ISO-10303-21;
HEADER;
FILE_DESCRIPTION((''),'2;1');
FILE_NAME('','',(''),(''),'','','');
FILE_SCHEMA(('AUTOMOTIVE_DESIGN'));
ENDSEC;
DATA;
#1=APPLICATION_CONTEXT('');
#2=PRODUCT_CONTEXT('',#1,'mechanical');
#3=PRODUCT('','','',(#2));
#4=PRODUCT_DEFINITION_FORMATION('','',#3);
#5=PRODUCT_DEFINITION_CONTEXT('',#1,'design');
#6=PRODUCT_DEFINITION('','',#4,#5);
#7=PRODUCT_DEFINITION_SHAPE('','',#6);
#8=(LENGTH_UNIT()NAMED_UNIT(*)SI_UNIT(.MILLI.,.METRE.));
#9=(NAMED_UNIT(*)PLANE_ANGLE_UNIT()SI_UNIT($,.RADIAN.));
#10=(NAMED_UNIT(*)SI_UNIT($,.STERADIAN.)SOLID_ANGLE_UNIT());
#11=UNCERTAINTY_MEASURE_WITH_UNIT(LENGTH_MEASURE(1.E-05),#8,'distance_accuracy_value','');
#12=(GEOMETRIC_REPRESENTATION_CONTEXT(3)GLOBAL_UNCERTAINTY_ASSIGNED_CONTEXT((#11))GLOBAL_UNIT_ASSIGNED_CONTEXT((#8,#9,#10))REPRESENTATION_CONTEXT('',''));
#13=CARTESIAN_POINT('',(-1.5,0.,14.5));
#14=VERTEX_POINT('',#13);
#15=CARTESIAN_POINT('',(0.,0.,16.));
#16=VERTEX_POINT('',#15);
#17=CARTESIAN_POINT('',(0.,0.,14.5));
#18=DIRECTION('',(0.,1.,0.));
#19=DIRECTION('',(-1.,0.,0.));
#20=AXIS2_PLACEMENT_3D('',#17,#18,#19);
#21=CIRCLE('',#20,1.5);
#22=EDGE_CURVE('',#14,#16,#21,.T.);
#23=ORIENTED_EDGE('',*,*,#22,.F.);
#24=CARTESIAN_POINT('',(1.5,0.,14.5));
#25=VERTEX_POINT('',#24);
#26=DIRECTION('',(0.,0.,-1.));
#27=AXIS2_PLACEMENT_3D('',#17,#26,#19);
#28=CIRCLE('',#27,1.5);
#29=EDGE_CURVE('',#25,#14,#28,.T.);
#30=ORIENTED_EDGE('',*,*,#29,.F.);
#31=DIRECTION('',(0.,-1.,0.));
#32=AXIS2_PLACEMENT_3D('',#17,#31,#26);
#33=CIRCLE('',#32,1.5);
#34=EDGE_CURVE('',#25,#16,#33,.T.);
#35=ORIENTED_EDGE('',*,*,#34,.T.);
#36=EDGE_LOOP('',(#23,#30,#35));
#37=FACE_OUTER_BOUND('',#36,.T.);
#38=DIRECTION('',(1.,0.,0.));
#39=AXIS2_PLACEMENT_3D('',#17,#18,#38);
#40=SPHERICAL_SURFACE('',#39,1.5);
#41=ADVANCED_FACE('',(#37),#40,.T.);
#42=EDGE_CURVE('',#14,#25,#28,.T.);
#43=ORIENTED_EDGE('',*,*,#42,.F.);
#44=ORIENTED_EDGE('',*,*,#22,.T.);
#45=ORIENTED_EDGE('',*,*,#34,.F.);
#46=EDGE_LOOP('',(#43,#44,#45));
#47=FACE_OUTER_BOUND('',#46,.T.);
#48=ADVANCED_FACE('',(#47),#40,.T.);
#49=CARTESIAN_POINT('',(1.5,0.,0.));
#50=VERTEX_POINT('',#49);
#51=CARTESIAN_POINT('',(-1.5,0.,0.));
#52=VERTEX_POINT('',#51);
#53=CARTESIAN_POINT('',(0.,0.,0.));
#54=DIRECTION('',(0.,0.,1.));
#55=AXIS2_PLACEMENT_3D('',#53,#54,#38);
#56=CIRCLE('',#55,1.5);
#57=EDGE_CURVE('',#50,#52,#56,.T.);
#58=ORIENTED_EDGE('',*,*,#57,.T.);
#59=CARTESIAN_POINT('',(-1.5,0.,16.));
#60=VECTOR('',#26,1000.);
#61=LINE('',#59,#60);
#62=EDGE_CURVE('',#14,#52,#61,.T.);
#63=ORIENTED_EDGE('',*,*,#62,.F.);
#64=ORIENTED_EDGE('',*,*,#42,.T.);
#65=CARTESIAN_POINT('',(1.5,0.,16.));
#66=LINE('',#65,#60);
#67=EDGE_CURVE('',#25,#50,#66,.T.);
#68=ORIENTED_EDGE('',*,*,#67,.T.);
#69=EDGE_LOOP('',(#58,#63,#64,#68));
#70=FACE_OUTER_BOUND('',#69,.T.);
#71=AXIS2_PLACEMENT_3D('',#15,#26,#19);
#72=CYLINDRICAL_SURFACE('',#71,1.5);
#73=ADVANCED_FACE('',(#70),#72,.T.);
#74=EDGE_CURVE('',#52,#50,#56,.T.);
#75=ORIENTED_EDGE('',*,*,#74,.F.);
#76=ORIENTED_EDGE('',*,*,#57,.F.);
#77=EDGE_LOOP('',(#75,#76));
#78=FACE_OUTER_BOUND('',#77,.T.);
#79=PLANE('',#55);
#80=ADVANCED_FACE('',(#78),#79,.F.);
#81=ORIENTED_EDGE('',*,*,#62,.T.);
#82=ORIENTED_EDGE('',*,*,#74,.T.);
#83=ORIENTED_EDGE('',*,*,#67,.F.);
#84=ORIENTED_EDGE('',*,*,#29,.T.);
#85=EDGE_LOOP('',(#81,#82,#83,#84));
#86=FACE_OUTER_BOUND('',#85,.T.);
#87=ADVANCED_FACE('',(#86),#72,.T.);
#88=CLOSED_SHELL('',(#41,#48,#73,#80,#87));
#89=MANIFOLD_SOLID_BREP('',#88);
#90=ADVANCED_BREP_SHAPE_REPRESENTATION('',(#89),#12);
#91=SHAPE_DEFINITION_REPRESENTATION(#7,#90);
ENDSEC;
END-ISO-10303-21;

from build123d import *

# Parameters (mm, degrees)
SKETCH1_R           = 1.5
BOSS_EXTRUDE1_DEPTH = 16
FILLET1_R           = 1.5


with BuildPart() as part:
    # Sketch1 → Boss-Extrude1 (new body)
    with BuildSketch(Plane.XY):
        Circle(SKETCH1_R)
    extrude(amount=BOSS_EXTRUDE1_DEPTH)

    # Fillet1
    fillet1_edges = [part.edges().sort_by_distance(p)[0] for p in [
        (-1.5, 0, 16),
    ]]
    fillet(fillet1_edges, radius=FILLET1_R)


solid = part.part
